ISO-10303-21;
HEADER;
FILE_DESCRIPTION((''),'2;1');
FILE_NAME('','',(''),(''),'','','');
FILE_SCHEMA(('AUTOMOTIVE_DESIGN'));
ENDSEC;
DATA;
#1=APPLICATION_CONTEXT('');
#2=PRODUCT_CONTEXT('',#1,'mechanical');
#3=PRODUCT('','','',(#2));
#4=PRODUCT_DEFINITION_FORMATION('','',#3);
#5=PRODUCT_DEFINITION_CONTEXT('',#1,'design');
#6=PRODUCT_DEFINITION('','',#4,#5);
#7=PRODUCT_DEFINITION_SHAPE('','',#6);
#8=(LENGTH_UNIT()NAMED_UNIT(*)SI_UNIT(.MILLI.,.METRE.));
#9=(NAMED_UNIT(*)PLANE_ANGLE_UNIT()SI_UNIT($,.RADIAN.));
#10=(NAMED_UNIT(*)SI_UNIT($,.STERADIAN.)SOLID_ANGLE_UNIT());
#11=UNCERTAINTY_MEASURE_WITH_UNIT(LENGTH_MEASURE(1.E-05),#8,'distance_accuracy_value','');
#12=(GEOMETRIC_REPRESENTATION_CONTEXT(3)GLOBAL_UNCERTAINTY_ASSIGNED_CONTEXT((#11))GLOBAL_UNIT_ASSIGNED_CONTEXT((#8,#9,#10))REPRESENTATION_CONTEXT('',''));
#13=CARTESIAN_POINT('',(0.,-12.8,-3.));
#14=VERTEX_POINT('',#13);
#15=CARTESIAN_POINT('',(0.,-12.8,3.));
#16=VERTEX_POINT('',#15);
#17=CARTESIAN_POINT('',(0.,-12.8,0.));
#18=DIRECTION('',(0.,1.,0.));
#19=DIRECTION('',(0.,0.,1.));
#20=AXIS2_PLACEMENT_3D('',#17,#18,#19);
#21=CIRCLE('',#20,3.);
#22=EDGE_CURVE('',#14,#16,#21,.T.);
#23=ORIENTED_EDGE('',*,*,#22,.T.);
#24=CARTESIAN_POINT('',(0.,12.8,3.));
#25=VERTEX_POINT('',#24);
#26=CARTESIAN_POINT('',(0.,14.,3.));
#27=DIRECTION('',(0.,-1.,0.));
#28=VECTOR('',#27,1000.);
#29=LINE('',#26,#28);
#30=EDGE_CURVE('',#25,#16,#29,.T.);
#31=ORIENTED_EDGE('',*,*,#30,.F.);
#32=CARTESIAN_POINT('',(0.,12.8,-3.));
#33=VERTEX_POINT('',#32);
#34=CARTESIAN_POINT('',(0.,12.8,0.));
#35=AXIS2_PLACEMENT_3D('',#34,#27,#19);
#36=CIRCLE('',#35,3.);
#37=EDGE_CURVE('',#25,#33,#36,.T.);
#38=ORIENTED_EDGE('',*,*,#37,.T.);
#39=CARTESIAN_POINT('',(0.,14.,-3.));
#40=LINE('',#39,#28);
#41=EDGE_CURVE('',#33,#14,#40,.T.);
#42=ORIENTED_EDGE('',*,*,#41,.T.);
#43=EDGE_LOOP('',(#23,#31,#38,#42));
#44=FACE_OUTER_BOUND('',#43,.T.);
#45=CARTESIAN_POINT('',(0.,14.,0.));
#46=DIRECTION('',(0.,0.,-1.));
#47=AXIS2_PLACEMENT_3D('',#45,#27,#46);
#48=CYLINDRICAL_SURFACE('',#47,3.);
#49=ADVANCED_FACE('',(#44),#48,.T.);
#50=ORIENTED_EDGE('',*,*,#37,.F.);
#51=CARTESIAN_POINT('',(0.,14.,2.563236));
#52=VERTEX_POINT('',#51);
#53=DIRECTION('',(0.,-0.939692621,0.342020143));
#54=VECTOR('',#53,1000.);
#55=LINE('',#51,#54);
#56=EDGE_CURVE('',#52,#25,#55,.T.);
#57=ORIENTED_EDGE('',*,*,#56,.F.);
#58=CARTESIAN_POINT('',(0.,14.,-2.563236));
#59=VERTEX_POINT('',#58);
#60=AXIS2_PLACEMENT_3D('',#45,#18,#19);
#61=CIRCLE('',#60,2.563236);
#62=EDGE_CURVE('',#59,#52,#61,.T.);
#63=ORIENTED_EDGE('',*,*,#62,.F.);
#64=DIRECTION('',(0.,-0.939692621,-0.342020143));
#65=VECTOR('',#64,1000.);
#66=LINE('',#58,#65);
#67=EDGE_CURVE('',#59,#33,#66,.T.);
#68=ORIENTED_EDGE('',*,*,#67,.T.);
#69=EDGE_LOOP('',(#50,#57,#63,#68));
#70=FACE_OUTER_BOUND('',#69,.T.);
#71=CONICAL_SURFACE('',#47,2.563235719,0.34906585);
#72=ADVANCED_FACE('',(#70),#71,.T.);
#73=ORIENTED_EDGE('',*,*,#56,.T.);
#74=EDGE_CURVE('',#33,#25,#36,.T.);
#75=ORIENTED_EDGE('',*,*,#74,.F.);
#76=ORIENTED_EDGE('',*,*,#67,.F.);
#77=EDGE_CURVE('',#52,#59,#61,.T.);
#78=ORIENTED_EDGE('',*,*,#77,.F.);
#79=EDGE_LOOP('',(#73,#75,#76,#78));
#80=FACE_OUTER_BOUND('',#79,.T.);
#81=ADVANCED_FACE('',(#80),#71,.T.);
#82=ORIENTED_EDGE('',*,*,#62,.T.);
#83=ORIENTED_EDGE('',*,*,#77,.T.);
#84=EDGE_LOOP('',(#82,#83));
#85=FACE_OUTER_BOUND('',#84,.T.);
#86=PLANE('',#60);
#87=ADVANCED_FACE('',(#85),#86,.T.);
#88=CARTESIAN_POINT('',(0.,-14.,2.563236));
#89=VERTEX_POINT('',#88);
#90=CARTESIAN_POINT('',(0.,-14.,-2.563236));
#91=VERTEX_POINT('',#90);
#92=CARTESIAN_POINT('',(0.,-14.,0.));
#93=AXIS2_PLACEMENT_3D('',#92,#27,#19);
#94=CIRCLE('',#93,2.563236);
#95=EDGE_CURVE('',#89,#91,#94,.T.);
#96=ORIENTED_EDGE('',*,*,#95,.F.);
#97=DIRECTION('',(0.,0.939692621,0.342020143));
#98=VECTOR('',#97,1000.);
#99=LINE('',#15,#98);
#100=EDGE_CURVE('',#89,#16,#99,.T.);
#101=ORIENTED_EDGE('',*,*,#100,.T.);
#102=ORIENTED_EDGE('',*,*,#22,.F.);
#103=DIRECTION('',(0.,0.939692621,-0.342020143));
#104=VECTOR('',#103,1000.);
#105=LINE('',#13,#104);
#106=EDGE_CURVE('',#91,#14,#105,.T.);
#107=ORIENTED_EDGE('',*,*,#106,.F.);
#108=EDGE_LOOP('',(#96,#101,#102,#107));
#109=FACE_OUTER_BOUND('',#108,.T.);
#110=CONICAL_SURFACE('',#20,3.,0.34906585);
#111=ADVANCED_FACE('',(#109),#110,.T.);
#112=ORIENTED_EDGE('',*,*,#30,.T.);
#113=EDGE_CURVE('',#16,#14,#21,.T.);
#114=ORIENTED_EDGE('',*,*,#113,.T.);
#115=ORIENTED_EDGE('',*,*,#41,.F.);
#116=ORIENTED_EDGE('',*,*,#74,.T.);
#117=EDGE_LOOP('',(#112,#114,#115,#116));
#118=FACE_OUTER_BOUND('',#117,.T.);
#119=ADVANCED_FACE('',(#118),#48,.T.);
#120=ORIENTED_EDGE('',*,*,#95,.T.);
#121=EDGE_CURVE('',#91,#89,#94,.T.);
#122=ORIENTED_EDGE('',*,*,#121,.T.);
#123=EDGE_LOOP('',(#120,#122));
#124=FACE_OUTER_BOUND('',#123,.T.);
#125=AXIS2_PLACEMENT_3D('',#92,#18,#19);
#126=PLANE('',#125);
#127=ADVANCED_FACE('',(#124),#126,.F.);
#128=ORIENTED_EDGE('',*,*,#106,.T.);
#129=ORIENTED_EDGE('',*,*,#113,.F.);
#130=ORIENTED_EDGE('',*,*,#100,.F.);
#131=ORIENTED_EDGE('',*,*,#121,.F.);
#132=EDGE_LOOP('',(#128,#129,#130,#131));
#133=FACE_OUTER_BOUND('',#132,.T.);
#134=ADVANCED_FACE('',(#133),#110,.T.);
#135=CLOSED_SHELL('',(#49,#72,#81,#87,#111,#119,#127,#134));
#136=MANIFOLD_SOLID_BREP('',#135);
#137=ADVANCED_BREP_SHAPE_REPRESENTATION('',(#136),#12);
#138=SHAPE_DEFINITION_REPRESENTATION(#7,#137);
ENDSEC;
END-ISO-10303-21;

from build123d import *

# Parameters (mm, degrees)
SKETCH1_R           = 3
BOSS_EXTRUDE1_DEPTH = 14
CHAMFER1_SIZE       = 1.2
CHAMFER1_SIZE2      = 0.436764281
CHAMFER2_SIZE       = 1.2
CHAMFER2_SIZE2      = 0.436764281


with BuildPart() as part:
    # Sketch1 → Boss-Extrude1 (new, symmetric)
    with BuildSketch(Plane(origin=(0, 0, 0), x_dir=(1, 0, 0), z_dir=(0, 1, 0))):
        with Locations(Location((0, 0, 0), (0, 0, 270))):
            Circle(SKETCH1_R)
    extrude(amount=BOSS_EXTRUDE1_DEPTH, both=True)

    # Chamfer1
    chamfer1_edges = [part.edges().sort_by_distance(p)[0] for p in [
        (0, 14, -3),
    ]]
    chamfer1_side = [part.faces().sort_by_distance(p)[0] for p in [
        (0, 0, -3),
    ]]
    chamfer(chamfer1_edges, length=CHAMFER1_SIZE, length2=CHAMFER1_SIZE2, reference=chamfer1_side[0])

    # Chamfer2
    chamfer2_edges = [part.edges().sort_by_distance(p)[0] for p in [
        (0, -14, -3),
    ]]
    chamfer2_side = [part.faces().sort_by_distance(p)[0] for p in [
        (0, -0.6, -3),
    ]]
    chamfer(chamfer2_edges, length=CHAMFER2_SIZE, length2=CHAMFER2_SIZE2, reference=chamfer2_side[0])


solid = part.part
